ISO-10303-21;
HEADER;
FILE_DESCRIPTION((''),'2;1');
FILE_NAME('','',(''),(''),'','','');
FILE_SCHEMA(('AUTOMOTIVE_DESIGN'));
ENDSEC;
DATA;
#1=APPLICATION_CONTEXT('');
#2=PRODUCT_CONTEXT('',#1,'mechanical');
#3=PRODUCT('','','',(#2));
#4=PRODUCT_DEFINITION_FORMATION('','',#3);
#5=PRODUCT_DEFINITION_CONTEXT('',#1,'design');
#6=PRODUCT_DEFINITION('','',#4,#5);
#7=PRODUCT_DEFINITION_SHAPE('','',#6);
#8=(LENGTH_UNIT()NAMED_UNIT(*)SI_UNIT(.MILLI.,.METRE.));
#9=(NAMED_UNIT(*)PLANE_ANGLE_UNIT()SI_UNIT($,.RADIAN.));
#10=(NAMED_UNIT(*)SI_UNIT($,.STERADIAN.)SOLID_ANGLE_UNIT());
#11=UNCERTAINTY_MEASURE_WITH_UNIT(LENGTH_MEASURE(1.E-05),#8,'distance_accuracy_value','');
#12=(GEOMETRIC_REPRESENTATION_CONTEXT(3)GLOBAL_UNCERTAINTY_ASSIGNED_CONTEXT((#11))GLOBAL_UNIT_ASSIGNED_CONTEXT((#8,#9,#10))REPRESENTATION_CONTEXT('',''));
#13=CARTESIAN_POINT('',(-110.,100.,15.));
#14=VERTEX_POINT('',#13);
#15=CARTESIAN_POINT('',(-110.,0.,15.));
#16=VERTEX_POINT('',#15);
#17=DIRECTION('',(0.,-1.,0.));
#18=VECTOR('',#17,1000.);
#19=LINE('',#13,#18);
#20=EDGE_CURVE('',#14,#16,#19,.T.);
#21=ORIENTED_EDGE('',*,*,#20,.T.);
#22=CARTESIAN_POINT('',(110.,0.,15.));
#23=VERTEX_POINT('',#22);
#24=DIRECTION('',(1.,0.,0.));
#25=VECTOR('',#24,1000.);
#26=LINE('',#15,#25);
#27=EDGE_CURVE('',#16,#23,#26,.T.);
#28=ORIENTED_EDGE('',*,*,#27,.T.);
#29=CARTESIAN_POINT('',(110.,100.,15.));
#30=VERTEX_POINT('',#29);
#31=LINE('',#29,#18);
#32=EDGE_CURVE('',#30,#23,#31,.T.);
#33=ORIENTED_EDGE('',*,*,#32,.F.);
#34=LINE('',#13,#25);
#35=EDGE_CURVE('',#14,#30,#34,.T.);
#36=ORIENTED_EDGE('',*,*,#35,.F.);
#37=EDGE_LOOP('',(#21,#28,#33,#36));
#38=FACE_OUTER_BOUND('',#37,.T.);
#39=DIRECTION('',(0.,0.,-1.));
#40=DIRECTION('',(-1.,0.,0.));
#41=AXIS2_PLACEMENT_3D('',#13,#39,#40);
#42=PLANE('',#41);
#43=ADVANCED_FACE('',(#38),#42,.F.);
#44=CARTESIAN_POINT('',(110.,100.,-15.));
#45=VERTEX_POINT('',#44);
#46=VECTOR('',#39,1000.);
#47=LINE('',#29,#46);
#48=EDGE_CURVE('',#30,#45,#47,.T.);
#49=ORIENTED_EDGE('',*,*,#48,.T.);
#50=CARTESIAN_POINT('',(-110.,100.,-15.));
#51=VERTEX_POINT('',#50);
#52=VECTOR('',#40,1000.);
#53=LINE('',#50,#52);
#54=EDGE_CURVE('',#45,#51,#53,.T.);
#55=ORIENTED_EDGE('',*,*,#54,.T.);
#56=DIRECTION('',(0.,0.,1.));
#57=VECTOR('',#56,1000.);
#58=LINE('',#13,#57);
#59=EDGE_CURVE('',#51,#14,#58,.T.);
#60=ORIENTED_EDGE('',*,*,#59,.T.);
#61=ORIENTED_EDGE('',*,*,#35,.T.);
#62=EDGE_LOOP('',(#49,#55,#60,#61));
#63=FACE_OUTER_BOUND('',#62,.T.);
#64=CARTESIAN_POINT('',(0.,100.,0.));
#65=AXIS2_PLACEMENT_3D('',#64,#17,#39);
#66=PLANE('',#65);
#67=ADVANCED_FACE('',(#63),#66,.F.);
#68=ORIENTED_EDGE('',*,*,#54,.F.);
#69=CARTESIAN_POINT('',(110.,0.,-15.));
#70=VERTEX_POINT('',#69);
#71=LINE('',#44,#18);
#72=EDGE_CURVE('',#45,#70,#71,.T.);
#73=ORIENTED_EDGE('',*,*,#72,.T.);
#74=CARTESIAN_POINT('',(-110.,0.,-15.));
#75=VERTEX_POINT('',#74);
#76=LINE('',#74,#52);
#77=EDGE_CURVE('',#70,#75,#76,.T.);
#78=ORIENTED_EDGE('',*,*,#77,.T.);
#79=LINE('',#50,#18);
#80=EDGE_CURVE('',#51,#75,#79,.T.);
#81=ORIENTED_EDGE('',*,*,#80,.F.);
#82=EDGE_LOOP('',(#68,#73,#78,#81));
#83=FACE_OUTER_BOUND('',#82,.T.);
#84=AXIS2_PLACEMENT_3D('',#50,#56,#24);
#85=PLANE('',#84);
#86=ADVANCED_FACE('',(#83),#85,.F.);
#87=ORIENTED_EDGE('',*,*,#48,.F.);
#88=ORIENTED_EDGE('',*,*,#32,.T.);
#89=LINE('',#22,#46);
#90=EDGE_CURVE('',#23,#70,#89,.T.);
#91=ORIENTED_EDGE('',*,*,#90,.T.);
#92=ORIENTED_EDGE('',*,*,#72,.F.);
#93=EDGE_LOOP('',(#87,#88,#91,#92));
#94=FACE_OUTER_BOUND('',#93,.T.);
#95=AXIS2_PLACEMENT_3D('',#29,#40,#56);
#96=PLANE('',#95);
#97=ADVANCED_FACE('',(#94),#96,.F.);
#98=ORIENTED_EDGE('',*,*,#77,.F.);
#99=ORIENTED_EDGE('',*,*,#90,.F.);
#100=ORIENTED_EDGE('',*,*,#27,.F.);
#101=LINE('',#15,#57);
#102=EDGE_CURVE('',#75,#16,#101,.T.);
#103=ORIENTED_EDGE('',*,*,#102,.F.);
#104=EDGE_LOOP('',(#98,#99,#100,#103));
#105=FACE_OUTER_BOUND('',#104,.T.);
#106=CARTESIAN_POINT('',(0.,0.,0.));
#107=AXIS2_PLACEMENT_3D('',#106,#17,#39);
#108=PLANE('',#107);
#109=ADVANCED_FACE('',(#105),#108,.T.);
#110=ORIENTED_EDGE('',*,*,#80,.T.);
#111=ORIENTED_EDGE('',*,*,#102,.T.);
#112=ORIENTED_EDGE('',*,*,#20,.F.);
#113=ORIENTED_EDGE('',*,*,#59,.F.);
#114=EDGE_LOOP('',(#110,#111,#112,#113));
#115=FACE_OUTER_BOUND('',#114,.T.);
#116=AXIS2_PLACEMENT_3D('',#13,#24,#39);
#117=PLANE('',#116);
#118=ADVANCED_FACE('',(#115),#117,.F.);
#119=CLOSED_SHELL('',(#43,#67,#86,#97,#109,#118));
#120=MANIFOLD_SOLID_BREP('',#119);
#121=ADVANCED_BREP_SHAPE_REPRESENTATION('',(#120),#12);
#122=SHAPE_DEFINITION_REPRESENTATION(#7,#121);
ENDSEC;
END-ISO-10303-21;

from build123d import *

# Parameters (mm, degrees)
SKETCH1_W           = 220
SKETCH1_H           = 30
BOSS_EXTRUDE1_DEPTH = 100


with BuildPart() as part:
    # Sketch1 → Boss-Extrude1 (new body)
    with BuildSketch(Plane(origin=(0, 0, 0), x_dir=(1, 0, 0), z_dir=(0, 1, 0))):
        Rectangle(SKETCH1_W, SKETCH1_H)
    extrude(amount=BOSS_EXTRUDE1_DEPTH)


solid = part.part
